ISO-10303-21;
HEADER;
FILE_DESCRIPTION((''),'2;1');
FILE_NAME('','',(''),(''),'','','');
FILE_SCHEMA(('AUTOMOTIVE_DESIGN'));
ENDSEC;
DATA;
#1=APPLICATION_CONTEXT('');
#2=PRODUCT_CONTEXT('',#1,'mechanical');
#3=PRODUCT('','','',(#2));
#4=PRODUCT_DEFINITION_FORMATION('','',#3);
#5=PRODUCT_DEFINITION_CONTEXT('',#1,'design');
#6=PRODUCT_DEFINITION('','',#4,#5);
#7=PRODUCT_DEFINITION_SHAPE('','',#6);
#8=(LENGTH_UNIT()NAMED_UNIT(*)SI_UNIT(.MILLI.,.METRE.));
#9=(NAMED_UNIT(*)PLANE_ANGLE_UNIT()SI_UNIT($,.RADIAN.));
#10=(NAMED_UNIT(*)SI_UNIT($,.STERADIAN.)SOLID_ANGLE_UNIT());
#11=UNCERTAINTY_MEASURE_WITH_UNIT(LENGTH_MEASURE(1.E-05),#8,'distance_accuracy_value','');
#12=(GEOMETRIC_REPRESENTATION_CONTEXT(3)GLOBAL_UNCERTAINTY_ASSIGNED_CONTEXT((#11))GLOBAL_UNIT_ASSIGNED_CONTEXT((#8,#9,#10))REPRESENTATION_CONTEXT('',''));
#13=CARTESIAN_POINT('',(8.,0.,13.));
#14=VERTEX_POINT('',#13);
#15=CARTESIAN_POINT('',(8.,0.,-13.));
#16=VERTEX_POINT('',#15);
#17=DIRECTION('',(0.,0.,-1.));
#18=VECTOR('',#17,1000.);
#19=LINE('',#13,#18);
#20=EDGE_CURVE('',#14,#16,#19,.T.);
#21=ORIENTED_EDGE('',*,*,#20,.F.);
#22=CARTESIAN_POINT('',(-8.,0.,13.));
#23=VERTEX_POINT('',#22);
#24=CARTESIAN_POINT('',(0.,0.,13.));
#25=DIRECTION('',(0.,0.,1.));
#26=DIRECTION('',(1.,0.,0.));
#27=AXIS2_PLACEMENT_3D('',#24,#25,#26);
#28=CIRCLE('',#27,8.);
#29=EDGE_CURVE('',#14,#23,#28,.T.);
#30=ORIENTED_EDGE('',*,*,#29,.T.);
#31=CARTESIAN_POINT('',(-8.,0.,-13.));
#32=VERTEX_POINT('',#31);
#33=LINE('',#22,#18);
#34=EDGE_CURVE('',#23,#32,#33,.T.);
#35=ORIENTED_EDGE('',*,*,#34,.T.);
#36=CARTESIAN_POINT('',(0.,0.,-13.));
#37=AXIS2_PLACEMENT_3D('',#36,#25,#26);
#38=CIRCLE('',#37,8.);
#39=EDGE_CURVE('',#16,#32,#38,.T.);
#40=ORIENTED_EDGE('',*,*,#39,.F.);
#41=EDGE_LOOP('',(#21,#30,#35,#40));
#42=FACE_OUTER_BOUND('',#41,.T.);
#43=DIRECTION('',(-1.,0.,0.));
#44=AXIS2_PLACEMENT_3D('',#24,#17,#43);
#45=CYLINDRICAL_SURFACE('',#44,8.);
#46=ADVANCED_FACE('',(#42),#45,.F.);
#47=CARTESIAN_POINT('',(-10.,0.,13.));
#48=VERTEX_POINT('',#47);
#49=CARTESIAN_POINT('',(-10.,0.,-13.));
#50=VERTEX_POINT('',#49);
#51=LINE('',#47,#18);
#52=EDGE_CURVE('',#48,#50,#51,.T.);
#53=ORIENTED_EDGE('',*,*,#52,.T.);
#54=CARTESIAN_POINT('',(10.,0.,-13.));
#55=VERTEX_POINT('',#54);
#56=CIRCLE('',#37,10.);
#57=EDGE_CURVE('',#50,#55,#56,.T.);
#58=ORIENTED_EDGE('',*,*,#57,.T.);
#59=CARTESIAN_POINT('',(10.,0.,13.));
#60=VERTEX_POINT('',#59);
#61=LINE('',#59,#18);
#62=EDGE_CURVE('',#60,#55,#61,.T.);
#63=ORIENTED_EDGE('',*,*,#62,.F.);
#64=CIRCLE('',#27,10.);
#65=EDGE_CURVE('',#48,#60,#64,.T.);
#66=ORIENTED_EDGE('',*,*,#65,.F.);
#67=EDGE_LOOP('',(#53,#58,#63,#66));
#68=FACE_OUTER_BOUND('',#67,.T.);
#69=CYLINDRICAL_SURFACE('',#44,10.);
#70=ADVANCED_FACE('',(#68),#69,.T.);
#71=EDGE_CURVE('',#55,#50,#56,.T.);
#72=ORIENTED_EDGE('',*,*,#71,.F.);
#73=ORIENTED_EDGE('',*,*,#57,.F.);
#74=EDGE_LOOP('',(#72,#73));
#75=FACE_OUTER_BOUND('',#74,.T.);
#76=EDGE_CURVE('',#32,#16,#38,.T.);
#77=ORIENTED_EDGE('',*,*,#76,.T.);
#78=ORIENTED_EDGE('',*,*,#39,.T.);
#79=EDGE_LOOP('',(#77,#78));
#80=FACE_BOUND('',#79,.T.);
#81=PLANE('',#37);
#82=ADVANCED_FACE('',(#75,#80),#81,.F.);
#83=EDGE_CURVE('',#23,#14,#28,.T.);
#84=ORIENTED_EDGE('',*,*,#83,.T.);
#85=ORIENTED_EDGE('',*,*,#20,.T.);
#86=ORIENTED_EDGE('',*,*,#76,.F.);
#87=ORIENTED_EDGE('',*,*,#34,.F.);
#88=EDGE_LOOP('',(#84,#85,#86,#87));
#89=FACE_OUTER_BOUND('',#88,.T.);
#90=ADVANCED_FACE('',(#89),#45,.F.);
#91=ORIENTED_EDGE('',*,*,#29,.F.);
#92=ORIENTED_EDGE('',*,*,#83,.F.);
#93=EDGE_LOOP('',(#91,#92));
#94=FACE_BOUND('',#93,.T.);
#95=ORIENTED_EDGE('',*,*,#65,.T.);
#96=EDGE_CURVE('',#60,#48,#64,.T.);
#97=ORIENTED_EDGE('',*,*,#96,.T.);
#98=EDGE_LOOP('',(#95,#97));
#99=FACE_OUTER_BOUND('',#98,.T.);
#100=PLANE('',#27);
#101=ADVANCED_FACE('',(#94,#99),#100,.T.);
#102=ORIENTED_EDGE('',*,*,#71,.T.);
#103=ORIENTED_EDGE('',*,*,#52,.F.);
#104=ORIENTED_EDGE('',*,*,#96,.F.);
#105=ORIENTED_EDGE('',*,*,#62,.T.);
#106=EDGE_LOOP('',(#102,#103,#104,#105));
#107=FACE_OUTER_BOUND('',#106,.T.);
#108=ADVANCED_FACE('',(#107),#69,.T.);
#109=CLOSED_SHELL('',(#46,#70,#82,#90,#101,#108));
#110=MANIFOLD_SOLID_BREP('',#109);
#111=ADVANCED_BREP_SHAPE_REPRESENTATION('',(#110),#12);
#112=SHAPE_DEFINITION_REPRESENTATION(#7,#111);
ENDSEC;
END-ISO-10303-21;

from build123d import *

# Parameters (mm, degrees)
SKETCH1_R           = 10
SKETCH1_R_2         = 8
BOSS_EXTRUDE1_DEPTH = 13


with BuildPart() as part:
    # Sketch1 → Boss-Extrude1 (new, symmetric)
    with BuildSketch(Plane.XY):
        with Locations(Location((0, 0, 0), (0, 0, 180))):
            Circle(SKETCH1_R)
        with Locations(Location((0, 0, 0), (0, 0, 180))):
            Circle(SKETCH1_R_2, mode=Mode.SUBTRACT)
    extrude(amount=BOSS_EXTRUDE1_DEPTH, both=True)


solid = part.part
